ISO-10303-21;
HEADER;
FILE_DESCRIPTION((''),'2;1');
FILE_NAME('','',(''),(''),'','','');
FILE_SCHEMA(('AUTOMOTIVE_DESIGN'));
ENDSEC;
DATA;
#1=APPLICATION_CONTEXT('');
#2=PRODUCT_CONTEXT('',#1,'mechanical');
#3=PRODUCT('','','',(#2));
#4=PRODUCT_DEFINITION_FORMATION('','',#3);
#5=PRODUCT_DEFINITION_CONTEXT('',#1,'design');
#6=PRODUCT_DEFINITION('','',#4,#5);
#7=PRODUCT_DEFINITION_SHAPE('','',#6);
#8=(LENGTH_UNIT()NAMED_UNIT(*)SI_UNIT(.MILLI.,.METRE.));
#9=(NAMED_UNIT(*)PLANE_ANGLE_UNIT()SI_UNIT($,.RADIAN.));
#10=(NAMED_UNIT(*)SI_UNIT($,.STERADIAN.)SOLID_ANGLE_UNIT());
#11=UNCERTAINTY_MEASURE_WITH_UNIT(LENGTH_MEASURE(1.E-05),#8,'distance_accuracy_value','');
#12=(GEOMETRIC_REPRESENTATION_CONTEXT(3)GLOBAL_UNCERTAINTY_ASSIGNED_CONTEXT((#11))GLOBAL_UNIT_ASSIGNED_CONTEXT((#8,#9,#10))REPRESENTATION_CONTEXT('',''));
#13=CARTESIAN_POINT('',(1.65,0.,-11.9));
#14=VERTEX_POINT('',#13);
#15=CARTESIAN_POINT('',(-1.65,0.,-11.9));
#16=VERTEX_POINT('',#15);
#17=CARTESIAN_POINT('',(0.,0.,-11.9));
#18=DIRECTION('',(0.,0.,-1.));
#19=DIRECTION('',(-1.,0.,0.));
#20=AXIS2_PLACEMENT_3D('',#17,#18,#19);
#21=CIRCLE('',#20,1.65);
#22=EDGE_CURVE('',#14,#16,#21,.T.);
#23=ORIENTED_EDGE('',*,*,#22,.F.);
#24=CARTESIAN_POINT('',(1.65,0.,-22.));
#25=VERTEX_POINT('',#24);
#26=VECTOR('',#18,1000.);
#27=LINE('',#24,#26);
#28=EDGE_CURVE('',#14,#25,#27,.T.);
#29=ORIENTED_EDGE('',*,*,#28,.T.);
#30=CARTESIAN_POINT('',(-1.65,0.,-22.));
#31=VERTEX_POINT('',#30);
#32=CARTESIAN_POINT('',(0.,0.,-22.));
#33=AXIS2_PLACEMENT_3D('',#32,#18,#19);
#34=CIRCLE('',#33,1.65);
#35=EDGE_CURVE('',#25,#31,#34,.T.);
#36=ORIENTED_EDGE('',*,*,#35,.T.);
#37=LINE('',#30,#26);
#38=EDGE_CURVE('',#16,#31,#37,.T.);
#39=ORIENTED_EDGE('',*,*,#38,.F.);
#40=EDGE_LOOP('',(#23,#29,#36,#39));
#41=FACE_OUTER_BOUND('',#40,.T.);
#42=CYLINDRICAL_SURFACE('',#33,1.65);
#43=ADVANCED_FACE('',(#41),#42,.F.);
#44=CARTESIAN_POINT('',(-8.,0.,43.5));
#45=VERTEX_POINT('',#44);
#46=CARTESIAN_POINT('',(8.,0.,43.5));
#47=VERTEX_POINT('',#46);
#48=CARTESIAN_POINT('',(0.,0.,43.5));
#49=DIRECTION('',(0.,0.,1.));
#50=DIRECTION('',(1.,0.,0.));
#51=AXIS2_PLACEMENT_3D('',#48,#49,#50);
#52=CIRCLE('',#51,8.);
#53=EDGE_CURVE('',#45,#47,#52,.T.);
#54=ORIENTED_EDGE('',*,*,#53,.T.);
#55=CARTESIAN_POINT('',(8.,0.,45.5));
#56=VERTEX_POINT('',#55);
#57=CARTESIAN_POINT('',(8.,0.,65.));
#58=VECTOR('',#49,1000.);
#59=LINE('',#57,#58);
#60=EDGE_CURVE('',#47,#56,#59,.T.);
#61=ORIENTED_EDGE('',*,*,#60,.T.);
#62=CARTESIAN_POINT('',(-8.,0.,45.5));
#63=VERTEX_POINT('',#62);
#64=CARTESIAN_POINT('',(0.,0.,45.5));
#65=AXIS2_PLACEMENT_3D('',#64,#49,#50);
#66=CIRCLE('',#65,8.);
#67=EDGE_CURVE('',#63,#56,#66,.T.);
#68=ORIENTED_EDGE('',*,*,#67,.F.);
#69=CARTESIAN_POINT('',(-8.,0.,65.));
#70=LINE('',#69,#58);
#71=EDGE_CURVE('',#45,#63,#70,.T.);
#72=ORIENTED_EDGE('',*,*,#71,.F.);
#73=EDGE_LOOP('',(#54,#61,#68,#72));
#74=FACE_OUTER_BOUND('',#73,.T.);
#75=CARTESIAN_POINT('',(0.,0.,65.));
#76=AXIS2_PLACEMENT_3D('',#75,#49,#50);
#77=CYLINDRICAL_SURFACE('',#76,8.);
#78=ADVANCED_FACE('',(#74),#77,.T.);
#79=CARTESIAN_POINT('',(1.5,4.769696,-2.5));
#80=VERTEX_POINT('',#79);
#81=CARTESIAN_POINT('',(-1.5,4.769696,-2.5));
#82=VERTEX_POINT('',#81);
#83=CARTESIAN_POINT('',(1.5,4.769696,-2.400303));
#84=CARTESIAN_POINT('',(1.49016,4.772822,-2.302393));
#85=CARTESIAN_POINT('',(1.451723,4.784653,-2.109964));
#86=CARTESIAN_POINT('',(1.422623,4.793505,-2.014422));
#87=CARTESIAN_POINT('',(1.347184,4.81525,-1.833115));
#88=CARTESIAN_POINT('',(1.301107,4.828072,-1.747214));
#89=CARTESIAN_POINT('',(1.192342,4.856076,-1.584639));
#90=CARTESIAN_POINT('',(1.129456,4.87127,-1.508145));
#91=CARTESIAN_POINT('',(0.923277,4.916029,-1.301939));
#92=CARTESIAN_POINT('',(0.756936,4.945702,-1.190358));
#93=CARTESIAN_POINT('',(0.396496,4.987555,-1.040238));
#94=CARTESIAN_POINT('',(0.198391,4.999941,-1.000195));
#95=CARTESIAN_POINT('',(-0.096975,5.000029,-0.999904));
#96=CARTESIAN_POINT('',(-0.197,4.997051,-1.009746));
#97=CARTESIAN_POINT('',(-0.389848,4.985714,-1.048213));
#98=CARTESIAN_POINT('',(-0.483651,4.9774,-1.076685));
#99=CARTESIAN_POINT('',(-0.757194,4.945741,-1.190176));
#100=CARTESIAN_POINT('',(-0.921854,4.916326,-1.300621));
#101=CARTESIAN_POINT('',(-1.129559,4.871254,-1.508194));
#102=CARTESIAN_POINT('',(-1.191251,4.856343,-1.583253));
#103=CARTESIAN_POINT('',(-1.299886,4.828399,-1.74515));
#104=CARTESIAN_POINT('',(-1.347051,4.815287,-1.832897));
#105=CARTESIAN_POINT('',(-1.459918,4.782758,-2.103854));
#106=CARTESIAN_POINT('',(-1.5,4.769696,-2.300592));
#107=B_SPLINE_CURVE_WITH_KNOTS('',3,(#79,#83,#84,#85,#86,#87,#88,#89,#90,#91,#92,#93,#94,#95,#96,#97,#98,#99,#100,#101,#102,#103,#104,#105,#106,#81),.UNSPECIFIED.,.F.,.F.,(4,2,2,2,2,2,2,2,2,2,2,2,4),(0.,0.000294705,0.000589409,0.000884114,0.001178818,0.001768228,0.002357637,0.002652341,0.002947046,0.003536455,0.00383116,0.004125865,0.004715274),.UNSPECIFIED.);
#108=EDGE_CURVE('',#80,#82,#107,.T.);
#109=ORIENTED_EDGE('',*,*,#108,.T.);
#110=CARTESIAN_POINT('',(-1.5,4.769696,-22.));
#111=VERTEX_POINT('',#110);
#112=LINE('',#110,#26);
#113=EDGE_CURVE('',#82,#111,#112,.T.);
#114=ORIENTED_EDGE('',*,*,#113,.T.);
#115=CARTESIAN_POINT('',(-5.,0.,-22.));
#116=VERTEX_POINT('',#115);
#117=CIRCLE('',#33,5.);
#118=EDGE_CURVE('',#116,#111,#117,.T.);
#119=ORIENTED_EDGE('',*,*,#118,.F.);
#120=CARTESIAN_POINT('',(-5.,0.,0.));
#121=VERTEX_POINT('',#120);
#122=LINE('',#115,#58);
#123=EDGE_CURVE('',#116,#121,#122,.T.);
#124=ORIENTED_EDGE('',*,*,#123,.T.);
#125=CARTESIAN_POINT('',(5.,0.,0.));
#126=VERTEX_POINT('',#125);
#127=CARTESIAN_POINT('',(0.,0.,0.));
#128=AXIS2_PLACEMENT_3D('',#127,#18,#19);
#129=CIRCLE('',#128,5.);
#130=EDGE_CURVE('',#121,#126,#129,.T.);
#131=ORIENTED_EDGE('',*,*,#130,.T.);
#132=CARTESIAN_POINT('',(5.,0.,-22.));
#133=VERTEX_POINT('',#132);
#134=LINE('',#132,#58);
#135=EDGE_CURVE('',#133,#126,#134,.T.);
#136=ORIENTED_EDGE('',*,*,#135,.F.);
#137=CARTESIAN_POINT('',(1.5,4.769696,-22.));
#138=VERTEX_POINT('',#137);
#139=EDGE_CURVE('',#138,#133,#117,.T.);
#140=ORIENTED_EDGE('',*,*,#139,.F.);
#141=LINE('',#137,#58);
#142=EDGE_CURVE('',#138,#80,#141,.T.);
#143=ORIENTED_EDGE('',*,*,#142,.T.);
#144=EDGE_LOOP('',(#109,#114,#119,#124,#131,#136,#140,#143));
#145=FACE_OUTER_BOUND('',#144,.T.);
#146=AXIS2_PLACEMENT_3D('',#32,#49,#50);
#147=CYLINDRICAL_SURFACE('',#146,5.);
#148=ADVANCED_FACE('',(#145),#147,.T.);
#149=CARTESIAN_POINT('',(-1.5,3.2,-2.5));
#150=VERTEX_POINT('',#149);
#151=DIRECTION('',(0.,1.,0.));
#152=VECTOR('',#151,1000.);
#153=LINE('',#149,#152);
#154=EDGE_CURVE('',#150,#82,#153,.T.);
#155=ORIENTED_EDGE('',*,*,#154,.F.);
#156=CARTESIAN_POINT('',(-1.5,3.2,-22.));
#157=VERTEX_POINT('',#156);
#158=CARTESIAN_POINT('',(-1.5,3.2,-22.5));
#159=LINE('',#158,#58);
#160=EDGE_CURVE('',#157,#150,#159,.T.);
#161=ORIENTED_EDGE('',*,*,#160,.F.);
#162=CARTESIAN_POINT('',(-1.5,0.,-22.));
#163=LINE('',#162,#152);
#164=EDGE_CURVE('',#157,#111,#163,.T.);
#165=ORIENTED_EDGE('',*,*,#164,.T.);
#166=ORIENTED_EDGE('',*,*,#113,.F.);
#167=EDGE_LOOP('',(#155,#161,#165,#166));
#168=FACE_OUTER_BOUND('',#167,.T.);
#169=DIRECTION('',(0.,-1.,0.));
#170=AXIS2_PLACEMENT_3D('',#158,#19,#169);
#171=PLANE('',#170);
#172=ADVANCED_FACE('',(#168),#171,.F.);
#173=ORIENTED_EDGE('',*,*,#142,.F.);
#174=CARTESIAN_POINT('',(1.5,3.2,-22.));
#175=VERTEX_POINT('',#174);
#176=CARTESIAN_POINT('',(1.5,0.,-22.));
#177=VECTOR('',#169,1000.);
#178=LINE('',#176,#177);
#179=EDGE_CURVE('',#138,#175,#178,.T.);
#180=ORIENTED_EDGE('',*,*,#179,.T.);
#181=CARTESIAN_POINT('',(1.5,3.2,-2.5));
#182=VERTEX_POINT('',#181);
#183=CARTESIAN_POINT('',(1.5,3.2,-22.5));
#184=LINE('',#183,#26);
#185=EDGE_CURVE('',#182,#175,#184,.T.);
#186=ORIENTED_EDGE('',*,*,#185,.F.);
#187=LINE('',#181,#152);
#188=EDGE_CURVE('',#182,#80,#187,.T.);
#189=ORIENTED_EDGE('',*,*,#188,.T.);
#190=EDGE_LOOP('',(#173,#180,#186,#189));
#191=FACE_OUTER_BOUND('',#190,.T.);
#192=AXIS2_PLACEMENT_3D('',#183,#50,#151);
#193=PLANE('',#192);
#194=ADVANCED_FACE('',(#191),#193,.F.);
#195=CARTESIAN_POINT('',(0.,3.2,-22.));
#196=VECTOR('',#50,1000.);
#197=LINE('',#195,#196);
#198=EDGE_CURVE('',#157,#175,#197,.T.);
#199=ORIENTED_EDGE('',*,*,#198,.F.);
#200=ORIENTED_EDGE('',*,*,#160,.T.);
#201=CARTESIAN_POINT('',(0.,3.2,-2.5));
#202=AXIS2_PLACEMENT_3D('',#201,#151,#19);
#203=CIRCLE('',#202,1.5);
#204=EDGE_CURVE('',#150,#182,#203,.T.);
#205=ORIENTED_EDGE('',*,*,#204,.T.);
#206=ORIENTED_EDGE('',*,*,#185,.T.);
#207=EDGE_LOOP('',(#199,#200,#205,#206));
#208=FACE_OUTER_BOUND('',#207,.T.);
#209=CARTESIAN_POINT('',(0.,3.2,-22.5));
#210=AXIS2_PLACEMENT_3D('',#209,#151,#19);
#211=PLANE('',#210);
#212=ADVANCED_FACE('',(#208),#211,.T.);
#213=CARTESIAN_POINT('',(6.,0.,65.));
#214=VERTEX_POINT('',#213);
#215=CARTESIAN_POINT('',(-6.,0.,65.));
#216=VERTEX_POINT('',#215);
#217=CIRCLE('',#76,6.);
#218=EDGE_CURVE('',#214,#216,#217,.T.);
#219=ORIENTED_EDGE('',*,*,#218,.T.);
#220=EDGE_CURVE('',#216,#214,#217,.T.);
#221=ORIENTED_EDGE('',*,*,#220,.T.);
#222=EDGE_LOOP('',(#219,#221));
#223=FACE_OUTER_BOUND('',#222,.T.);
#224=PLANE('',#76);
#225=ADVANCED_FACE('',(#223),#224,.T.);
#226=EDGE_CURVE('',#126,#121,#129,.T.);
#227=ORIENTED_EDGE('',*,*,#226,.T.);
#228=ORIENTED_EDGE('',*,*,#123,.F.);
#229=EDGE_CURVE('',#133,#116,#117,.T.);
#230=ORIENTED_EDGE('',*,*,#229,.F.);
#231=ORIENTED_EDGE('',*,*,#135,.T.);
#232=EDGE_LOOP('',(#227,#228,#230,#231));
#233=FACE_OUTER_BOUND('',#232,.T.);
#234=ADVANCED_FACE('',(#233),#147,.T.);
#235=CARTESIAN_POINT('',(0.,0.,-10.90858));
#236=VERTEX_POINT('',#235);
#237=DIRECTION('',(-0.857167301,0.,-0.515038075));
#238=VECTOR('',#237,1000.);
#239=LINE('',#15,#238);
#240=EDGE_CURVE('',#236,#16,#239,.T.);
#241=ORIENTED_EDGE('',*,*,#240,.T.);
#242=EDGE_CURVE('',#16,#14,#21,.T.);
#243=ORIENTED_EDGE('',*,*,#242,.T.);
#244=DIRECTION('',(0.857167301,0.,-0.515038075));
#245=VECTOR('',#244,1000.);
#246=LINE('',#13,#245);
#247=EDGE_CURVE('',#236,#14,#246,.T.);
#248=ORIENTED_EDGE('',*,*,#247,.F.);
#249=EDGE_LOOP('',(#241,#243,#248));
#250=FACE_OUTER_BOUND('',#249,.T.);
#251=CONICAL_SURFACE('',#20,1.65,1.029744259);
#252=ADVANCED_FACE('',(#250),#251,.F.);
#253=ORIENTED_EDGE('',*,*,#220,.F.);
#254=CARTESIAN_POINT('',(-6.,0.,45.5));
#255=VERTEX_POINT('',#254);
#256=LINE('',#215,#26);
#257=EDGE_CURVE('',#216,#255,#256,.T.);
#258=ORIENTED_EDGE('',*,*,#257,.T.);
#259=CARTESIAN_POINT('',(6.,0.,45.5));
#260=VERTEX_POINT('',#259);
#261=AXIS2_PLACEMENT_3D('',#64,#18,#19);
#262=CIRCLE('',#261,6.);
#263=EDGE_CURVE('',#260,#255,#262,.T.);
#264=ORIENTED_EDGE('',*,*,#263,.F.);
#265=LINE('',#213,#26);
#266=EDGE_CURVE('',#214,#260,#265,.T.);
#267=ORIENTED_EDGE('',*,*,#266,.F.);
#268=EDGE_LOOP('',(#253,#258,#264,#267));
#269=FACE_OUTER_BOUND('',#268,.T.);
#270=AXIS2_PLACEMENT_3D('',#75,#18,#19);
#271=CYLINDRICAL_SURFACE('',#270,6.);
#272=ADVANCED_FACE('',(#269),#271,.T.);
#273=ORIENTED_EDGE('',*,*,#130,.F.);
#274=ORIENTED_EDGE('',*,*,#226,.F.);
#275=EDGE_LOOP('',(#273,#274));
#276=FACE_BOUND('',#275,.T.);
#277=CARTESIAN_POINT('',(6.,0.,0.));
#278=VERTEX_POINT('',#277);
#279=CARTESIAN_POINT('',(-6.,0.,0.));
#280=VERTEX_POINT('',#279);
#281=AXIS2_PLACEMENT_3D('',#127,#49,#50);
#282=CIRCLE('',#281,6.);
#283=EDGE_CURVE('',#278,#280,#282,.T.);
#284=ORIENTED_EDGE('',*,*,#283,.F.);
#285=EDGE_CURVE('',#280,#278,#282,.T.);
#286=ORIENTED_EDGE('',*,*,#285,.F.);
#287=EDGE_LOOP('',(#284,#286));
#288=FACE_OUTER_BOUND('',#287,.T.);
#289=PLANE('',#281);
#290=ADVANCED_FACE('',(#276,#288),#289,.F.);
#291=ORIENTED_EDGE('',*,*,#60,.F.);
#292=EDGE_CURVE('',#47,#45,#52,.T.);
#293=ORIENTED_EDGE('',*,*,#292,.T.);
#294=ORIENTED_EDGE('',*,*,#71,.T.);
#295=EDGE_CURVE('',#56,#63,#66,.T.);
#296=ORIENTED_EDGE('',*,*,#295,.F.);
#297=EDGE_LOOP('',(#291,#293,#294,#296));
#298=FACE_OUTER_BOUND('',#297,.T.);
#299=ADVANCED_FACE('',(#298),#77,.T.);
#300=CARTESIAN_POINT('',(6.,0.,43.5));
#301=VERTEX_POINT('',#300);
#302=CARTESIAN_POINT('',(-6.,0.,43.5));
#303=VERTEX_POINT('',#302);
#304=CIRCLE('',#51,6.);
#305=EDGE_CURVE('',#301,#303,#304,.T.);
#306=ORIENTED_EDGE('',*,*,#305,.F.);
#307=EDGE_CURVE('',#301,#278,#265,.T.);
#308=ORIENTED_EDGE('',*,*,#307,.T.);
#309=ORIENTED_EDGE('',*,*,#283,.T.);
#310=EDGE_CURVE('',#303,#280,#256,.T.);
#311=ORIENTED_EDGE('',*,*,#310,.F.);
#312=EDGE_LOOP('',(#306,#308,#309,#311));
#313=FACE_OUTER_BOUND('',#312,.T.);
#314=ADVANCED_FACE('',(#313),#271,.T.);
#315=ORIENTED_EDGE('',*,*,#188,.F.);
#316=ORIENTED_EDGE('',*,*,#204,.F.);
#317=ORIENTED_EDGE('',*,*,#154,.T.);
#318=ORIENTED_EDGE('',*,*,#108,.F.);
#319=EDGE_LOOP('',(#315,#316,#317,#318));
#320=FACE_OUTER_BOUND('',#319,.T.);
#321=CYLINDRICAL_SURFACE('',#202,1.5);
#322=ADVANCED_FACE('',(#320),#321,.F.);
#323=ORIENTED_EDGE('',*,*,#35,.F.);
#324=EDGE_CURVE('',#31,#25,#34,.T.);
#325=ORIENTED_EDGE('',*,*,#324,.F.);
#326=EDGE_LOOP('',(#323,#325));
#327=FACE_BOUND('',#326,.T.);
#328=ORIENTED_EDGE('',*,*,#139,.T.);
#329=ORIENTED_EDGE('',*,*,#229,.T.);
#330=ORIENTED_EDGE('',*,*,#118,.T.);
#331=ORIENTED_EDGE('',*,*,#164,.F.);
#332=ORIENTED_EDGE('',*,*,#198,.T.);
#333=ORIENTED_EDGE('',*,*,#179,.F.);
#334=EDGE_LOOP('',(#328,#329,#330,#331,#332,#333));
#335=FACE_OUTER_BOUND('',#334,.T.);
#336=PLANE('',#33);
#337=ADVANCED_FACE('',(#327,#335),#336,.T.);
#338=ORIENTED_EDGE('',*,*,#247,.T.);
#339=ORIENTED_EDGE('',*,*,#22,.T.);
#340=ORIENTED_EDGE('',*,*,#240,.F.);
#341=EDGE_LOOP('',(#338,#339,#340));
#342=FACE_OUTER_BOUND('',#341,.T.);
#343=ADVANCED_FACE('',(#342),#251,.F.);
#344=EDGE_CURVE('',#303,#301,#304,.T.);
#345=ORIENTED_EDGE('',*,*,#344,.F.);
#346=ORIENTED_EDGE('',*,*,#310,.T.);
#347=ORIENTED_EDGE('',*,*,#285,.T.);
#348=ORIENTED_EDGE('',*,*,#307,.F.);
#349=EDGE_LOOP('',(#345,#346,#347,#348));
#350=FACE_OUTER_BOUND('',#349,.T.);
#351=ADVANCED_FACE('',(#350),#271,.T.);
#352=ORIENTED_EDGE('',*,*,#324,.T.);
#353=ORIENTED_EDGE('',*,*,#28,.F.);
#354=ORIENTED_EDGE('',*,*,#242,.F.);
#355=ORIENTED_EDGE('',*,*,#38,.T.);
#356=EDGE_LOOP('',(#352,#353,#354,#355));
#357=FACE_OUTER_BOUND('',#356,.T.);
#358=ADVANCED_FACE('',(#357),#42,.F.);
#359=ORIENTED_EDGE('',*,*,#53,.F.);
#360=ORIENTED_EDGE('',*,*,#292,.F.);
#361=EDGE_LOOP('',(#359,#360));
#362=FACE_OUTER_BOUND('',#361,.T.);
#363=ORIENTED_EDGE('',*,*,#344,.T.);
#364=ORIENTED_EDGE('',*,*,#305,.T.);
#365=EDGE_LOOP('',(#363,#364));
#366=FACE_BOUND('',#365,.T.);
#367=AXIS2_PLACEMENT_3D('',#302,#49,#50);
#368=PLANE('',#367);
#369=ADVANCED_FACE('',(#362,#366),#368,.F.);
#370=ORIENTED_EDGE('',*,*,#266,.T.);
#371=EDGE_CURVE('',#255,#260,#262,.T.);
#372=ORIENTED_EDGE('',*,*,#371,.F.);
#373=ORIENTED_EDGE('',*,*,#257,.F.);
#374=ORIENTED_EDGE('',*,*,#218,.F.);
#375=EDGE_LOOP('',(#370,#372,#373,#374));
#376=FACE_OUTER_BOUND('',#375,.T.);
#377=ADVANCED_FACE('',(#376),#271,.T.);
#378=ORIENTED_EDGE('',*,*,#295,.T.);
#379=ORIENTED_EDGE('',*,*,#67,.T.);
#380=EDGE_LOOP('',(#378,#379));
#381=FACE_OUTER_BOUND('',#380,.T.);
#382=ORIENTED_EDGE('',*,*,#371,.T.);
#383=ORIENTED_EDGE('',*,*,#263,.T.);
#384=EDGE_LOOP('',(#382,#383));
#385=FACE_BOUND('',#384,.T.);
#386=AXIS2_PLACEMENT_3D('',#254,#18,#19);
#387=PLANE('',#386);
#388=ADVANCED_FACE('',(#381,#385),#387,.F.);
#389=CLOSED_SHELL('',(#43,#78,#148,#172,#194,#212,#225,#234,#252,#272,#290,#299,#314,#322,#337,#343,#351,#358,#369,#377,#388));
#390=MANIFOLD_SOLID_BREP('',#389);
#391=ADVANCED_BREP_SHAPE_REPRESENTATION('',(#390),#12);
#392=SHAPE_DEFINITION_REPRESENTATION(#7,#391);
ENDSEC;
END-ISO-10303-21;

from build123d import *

# Parameters (mm, degrees)
SKETCH_1_R             = 6
EXTRUDE_1_DEPTH        = 65
SKETCH_2_R             = 5
EXTRUDE_2_DEPTH        = 22
SKETCH_3_W             = 2
SKETCH_3_H             = 2
ZJCQC_DEPTH            = 1.8
HOLE_WIZARD_M4_1_D     = 3.3
HOLE_WIZARD_M4_1_DEPTH = 10.1
HOLE_WIZARD_M4_1_TIP   = 0.991420021


with BuildPart() as part:
    # 草图1 → 凸台-拉伸1 (new body)
    with BuildSketch(Plane.XY):
        Circle(SKETCH_1_R)
    extrude(amount=EXTRUDE_1_DEPTH)

    # 草图2 → 凸台-拉伸2 (add)
    with BuildSketch(Plane(origin=(0, 0, 0), x_dir=(-1, 0, 0), z_dir=(0, 0, -1))):
        Circle(SKETCH_2_R)
    extrude(amount=EXTRUDE_2_DEPTH)

    # 草图3 → 旋转1 (revolve)
    with BuildSketch(Plane(origin=(0, 0, 0), x_dir=(1, 0, 0), z_dir=(0, 1, 0)), mode=Mode.PRIVATE) as revolve_1_sk:
        with Locations((-7, -44.5)):
            Rectangle(SKETCH_3_W, SKETCH_3_H)
    revolve(revolve_1_sk.sketch.rotate(Axis((0, 0, 65), (0, 0, -1)), 180), axis=Axis((0, 0, 65), (0, 0, -1)))

    # MyToolsZJC → ZJCQC (cut)
    with BuildSketch(Plane(origin=(0, 5, -22), x_dir=(0, 0, 1), z_dir=(0, 1, 0))):
        with BuildLine():
            Line((-0.5, 1.5), (19.5, 1.5))
            ThreePointArc((19.5, 1.5), (21, 0), (19.5, -1.5))
            Line((19.5, -1.5), (-0.5, -1.5))
            ThreePointArc((-0.5, -1.5), (-2, 0), (-0.5, 1.5))
        make_face()
    extrude(amount=-ZJCQC_DEPTH, mode=Mode.SUBTRACT)

    # M4 螺纹孔1
    with Locations(Plane(origin=(0, 0, -22), x_dir=(-1, 0, 0), z_dir=(0, 0, -1))):
        with Locations((0, 0)):
            Hole(HOLE_WIZARD_M4_1_D / 2, depth=HOLE_WIZARD_M4_1_DEPTH)
            with Locations((0, 0, -(HOLE_WIZARD_M4_1_DEPTH + HOLE_WIZARD_M4_1_TIP / 2))):  # 118° drill point
                Cone(0, HOLE_WIZARD_M4_1_D / 2, HOLE_WIZARD_M4_1_TIP, mode=Mode.SUBTRACT)


solid = part.part
